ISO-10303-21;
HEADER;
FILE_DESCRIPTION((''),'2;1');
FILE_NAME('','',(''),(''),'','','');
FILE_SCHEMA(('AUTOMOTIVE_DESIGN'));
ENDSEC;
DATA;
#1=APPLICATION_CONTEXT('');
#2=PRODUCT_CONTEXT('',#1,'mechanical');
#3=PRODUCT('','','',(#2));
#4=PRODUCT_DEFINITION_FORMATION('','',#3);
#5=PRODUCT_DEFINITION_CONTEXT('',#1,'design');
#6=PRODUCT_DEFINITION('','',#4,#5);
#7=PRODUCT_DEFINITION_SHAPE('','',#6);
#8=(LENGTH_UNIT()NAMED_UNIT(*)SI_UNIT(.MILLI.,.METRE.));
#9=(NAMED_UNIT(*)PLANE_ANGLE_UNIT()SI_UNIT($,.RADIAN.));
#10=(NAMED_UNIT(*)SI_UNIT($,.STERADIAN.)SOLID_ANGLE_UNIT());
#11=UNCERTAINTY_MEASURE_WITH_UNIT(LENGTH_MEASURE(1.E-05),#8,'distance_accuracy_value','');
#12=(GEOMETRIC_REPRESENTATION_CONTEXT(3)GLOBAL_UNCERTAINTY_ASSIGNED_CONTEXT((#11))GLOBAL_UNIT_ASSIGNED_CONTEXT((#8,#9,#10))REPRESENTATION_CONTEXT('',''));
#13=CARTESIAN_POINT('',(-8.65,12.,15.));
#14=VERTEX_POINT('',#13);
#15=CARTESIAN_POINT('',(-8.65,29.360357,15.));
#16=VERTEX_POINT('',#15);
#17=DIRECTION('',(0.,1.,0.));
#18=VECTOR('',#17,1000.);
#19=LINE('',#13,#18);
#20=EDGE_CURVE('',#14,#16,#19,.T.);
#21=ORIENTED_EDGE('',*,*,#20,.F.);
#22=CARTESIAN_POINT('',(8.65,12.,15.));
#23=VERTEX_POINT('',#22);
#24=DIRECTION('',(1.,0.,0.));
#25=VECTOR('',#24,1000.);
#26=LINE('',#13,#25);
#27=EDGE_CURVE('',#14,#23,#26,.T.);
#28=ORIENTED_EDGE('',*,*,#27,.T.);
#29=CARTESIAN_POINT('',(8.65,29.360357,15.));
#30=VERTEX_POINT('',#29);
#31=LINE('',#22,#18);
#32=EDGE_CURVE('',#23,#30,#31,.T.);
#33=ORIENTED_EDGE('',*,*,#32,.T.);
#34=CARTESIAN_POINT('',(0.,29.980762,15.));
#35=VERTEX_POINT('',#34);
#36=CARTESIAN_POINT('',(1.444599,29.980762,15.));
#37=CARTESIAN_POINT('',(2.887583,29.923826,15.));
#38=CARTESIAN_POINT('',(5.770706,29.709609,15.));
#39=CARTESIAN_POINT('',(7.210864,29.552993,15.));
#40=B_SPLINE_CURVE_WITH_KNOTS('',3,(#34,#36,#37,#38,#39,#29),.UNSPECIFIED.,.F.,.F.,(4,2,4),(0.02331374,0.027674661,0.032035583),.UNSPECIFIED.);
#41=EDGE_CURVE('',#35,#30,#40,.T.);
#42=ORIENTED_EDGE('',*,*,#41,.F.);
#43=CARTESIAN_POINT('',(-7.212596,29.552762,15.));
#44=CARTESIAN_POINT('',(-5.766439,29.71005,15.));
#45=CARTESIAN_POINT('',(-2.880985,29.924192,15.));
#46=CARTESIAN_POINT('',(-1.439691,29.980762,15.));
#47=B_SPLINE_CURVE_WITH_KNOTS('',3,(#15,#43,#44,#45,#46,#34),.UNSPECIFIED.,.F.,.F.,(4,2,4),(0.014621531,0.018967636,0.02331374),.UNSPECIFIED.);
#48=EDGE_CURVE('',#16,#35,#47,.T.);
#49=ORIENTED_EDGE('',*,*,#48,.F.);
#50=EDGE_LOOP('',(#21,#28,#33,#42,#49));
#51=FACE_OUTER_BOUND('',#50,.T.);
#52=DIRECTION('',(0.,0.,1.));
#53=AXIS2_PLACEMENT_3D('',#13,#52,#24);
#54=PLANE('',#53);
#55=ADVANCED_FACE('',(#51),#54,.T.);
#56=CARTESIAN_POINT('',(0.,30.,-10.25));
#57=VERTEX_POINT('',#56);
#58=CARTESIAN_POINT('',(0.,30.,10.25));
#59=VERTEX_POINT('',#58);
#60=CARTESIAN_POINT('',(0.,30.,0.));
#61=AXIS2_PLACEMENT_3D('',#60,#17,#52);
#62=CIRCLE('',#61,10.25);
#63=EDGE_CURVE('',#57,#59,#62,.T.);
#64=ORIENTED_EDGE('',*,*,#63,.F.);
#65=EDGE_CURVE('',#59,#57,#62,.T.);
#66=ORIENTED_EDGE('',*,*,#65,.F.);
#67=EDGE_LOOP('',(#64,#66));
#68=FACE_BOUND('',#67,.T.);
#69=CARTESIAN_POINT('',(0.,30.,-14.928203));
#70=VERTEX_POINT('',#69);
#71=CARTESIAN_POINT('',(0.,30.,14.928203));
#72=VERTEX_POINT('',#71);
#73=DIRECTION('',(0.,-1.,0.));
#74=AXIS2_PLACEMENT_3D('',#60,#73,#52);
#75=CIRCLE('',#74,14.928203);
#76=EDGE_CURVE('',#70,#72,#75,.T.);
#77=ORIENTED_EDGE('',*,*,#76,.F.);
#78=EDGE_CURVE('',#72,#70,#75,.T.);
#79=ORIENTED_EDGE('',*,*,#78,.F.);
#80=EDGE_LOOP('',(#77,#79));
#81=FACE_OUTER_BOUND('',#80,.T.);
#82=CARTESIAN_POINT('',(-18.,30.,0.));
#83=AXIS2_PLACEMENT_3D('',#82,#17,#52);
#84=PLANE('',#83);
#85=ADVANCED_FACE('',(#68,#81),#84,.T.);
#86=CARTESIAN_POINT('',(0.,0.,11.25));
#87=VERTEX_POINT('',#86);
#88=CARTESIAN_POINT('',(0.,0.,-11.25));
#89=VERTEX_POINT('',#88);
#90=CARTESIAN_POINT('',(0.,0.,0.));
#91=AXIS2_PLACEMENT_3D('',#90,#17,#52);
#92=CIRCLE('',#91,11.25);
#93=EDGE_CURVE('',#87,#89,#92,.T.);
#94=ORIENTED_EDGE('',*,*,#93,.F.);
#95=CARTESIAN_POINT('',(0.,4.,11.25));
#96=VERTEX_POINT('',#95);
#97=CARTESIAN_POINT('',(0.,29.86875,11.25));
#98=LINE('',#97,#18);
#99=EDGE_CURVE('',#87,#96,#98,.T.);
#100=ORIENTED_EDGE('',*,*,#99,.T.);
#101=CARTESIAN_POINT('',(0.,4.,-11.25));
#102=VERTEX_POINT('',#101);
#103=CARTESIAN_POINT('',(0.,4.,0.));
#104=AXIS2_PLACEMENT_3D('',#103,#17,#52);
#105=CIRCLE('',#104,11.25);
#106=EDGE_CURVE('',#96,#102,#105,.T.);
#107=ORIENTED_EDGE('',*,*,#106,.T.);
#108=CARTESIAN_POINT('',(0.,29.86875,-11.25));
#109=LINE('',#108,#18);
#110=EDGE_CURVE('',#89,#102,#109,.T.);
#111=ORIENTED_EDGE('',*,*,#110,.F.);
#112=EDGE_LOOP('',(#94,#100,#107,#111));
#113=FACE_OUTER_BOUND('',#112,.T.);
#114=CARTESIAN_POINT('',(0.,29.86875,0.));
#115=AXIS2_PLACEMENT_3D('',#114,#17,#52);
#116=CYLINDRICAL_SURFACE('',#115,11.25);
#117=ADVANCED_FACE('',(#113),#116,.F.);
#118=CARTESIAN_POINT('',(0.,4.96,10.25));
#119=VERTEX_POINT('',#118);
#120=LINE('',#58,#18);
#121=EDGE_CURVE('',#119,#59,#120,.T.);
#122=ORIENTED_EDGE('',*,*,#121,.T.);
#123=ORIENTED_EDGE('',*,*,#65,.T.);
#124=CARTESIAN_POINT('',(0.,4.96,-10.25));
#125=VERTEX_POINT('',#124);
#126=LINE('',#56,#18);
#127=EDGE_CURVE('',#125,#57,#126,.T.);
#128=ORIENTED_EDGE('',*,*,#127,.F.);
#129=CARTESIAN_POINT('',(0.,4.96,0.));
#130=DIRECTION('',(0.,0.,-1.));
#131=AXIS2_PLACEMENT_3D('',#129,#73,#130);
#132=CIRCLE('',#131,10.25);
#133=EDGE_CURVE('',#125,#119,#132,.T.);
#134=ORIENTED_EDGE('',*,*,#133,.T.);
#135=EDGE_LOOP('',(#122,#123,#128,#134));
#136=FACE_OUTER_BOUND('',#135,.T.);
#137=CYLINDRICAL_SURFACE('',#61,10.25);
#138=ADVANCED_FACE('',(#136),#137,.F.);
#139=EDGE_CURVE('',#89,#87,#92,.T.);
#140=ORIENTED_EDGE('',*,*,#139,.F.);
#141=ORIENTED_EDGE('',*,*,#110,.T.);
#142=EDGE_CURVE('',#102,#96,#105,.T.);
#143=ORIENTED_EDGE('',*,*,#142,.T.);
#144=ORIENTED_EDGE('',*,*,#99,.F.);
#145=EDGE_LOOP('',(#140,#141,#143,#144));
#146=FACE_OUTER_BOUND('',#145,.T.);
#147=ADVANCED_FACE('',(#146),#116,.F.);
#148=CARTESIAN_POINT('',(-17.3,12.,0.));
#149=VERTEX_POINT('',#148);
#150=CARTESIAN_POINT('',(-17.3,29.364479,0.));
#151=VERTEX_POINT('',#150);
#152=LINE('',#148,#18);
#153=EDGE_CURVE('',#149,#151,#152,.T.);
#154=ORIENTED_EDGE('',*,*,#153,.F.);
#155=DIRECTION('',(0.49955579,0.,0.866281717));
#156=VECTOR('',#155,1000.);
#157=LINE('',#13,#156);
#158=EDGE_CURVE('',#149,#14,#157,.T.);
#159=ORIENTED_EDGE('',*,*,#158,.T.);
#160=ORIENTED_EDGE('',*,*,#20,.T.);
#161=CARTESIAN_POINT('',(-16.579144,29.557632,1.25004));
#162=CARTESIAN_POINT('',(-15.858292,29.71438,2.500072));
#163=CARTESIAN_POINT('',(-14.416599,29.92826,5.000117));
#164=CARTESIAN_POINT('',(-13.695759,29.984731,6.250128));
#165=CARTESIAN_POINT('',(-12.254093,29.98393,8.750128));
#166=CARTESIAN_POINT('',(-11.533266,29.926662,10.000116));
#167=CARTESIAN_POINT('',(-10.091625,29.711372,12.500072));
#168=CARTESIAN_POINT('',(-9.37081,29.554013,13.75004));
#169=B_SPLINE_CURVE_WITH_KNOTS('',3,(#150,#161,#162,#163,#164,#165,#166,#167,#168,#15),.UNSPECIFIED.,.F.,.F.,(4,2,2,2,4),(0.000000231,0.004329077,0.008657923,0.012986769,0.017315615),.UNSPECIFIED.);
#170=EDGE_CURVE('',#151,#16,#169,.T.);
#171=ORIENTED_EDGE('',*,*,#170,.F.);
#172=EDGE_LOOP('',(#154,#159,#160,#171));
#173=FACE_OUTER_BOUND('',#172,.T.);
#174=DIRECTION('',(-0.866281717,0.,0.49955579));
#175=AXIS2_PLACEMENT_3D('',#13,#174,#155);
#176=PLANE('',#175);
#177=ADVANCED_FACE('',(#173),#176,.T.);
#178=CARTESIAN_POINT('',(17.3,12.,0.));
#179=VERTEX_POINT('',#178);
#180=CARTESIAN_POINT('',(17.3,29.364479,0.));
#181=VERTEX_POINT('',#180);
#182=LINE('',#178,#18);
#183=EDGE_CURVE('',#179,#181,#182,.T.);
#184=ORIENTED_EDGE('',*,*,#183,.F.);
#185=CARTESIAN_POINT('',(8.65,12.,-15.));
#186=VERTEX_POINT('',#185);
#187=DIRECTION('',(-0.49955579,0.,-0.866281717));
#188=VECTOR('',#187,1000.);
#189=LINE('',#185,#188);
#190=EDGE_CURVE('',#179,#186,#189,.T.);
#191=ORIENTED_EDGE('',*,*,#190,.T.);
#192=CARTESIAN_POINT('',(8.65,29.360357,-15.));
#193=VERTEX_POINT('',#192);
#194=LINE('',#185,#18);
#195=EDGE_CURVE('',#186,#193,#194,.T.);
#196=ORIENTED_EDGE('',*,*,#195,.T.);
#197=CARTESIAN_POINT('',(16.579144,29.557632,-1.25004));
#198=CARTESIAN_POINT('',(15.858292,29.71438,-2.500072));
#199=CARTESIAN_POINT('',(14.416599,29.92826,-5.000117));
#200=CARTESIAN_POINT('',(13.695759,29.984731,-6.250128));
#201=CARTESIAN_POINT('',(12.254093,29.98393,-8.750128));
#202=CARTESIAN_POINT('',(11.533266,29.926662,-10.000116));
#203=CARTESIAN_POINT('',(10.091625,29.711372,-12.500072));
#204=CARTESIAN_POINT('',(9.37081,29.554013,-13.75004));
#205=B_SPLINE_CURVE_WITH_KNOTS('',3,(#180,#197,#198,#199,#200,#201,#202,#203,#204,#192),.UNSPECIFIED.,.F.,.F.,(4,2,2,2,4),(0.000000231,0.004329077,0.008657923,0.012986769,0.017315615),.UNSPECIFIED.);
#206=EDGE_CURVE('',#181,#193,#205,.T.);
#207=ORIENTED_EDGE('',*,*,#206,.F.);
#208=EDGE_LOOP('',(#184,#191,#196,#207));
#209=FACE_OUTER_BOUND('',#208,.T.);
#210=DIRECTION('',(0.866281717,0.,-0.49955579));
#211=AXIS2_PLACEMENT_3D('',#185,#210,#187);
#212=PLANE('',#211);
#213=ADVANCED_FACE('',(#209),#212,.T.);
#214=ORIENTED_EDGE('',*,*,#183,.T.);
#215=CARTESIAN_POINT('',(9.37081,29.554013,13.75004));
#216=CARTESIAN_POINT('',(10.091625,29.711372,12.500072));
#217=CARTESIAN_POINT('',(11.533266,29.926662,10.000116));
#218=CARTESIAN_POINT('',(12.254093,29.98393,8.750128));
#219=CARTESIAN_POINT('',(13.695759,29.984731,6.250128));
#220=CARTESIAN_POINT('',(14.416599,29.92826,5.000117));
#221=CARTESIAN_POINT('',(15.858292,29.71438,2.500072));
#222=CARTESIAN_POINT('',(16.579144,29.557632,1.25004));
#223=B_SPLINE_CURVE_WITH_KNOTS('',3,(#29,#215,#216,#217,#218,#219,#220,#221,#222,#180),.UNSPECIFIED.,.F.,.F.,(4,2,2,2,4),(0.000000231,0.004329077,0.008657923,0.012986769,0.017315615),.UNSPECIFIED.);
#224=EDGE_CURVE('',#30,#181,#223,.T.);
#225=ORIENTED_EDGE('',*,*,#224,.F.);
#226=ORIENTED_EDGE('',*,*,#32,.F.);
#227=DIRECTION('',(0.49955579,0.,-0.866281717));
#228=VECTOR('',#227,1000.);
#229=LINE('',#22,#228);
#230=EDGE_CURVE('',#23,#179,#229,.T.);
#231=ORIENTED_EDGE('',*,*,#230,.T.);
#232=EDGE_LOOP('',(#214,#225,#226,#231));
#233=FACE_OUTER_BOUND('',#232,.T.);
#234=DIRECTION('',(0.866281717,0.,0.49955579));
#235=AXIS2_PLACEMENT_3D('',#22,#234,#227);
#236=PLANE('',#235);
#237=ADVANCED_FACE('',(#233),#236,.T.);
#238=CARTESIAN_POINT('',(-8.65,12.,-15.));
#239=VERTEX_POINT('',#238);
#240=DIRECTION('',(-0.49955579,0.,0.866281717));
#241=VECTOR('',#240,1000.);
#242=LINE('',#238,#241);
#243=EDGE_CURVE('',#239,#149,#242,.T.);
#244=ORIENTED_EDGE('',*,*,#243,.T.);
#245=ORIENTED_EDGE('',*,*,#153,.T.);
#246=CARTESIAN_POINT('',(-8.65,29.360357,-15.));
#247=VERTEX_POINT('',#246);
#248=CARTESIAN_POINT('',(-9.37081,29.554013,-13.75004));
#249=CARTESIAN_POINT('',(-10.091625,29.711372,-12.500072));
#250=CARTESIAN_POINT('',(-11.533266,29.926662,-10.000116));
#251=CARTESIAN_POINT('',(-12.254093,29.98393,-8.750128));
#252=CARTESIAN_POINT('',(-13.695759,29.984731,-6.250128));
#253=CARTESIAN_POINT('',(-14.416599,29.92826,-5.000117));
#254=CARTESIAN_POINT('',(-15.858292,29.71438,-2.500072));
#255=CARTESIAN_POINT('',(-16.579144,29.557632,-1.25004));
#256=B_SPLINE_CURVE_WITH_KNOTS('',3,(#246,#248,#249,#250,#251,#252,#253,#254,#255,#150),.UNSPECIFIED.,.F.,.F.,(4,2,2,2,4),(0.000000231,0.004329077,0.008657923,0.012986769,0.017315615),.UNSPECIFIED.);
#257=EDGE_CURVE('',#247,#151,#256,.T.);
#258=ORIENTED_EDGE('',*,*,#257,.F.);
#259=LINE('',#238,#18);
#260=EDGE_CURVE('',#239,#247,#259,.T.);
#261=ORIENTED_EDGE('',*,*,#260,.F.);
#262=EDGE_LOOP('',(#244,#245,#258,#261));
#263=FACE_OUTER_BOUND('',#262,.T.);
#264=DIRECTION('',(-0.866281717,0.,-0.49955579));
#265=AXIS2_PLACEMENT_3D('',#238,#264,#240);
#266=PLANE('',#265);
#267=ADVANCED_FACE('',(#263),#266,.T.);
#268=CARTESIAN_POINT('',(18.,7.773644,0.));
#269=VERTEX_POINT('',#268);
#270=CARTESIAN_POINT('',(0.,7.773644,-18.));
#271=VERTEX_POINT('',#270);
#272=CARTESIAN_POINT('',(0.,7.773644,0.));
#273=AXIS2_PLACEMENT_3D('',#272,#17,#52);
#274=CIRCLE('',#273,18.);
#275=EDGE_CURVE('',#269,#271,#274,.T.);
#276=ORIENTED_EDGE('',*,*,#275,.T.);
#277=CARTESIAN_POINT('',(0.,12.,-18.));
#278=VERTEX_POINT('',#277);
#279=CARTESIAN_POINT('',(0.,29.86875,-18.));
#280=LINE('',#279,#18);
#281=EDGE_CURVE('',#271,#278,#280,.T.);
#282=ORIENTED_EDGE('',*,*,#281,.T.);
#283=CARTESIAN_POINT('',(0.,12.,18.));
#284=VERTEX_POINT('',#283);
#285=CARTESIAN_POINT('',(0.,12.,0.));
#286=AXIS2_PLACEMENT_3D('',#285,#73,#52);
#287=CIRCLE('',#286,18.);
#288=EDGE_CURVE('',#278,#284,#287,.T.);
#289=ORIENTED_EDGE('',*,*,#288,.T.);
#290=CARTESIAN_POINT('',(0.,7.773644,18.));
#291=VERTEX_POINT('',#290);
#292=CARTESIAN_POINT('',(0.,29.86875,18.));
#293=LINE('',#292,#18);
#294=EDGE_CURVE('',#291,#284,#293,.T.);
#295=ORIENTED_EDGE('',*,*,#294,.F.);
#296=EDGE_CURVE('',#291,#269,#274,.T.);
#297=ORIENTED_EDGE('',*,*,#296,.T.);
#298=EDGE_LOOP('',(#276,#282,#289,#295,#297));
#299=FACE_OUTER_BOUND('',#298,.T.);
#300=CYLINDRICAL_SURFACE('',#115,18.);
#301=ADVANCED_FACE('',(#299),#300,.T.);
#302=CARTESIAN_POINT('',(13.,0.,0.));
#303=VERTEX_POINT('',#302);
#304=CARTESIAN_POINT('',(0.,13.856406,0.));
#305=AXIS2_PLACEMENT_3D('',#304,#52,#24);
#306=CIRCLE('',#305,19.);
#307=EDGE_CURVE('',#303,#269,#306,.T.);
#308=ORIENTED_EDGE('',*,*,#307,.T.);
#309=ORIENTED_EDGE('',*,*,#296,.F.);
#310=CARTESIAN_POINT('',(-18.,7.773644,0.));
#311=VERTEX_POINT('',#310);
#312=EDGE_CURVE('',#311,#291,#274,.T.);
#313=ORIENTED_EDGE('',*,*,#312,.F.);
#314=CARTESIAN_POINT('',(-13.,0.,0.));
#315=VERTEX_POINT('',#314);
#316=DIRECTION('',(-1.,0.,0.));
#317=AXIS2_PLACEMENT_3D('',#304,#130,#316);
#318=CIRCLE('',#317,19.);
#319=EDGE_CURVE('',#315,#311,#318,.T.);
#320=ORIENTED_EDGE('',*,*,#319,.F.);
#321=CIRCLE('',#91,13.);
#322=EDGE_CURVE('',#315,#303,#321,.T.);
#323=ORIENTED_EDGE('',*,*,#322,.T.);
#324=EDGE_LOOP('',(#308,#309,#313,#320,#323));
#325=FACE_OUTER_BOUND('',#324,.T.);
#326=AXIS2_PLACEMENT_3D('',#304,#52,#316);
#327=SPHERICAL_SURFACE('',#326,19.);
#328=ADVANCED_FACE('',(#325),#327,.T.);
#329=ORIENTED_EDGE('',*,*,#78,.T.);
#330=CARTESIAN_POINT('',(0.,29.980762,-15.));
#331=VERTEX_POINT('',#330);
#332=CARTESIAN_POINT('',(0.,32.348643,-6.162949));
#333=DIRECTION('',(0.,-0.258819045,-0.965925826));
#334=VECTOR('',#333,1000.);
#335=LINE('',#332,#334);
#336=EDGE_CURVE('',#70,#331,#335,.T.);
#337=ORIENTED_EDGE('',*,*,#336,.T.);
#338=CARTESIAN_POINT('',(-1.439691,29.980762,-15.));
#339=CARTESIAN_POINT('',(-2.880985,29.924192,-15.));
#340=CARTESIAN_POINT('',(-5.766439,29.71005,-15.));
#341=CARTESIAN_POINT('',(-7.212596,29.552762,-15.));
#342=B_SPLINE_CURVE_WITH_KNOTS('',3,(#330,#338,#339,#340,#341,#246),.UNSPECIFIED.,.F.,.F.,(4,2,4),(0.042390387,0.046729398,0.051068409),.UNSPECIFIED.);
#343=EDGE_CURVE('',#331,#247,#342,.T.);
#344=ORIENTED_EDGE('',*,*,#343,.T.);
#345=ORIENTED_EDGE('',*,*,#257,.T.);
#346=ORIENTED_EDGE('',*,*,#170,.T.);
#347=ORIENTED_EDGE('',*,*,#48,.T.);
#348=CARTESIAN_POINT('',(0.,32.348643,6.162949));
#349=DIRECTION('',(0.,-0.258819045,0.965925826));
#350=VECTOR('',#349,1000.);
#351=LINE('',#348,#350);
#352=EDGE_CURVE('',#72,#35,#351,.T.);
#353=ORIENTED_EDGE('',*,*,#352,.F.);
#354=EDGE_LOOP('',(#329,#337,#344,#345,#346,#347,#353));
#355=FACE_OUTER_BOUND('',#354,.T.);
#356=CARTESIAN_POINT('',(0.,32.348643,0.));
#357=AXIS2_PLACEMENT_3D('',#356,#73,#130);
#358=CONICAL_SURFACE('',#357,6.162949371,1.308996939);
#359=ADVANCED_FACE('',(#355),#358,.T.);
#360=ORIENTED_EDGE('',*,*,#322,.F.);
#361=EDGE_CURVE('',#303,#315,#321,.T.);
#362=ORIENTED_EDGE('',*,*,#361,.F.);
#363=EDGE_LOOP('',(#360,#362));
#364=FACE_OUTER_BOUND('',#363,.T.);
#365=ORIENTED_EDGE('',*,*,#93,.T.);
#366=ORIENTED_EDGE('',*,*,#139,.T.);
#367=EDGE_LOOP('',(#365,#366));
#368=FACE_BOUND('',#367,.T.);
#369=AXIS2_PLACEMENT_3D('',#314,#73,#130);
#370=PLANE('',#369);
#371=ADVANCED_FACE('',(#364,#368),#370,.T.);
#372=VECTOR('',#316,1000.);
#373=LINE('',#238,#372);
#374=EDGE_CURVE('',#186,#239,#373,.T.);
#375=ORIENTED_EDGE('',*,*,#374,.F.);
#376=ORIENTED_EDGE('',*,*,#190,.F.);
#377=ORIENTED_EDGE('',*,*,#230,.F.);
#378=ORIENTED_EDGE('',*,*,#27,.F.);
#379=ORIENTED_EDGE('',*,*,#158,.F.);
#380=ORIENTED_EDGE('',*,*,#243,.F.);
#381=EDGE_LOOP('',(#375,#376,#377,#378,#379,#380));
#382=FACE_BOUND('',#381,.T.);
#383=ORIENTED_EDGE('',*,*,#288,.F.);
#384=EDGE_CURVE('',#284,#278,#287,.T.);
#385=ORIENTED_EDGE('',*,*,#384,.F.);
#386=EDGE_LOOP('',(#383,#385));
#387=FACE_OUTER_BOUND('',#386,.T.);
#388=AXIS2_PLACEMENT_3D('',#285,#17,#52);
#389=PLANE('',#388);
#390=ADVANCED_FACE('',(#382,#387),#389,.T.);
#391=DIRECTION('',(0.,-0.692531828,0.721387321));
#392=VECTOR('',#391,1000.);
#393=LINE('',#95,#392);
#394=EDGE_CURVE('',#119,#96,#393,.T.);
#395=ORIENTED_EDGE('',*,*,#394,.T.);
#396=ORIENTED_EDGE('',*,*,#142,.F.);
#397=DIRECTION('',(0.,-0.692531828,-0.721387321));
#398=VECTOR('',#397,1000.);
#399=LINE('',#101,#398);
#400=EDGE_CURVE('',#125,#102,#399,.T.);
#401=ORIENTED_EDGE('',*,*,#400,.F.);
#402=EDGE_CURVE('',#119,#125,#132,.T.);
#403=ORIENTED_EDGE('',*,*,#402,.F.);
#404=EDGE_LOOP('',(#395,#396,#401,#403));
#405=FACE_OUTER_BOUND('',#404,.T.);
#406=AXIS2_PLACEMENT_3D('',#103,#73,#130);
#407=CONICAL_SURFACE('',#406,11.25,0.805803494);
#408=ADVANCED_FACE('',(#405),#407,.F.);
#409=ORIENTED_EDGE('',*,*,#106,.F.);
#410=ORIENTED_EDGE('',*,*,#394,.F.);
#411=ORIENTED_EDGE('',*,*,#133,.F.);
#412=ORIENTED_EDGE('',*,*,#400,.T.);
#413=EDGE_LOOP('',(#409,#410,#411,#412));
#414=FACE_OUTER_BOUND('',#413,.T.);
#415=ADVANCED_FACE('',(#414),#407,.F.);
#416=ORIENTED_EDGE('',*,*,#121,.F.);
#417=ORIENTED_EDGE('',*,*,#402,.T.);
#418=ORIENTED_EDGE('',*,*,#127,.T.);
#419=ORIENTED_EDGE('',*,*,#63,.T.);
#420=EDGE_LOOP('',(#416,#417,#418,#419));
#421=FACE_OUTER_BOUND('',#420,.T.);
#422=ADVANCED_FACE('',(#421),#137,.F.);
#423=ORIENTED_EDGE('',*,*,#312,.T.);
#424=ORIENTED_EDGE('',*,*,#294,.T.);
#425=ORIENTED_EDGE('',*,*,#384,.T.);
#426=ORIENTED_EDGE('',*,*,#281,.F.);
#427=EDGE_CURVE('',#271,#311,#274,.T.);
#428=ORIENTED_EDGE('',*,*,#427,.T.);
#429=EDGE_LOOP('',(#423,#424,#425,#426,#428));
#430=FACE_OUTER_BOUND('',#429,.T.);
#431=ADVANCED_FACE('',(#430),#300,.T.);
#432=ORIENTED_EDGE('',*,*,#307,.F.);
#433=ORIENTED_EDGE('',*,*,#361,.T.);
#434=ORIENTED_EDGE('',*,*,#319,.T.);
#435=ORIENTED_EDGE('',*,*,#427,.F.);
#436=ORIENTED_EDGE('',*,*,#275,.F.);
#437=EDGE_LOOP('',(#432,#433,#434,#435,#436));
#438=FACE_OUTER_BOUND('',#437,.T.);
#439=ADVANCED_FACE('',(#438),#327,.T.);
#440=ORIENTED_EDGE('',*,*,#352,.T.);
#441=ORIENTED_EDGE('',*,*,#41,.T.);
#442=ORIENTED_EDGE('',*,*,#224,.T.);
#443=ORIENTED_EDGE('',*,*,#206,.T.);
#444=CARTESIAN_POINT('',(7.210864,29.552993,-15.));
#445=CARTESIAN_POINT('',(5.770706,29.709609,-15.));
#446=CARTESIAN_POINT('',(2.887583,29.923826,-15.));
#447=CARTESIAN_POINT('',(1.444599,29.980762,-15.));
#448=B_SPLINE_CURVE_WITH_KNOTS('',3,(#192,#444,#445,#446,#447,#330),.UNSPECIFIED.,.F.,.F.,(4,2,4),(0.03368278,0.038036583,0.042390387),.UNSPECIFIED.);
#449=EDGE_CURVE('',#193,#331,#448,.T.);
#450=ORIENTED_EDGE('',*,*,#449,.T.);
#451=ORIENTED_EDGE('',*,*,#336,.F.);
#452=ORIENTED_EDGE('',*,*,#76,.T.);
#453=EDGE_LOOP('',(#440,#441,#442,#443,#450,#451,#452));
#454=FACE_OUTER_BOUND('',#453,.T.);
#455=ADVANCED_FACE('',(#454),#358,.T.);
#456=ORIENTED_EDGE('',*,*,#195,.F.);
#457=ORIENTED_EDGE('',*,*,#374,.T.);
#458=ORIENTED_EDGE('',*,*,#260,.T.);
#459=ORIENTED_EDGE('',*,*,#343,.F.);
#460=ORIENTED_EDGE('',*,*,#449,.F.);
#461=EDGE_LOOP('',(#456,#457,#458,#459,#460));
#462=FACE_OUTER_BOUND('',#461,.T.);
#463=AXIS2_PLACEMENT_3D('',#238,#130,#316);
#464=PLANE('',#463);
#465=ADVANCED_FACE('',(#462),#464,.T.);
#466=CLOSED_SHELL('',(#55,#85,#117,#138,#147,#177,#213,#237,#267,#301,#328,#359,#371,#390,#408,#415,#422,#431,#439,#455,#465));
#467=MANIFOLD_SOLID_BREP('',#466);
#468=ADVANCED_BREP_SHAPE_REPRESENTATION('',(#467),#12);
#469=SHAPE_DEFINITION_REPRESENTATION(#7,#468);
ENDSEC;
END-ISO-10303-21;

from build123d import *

# Parameters (mm, degrees)
M22X1_5_1_D         = 20.5
SKETCH_4_OUTSIDE_W  = 49.818
SKETCH_4_OUTSIDE_H  = 49.818
CUT_EXTRUDE_1_DEPTH = 18


with BuildPart() as part:
    # 草图1 → 旋转1 (revolve)
    with BuildSketch(Plane.XY, mode=Mode.PRIVATE) as revolve_1_sk:
        with BuildLine():
            Line((-18, 7.77364393), (-18, 30))
            Line((-18, 30), (-10, 30))
            Line((-10, 30), (-10, 5.2))
            Line((-10, 5.2), (-11.25, 4))
            Line((-11.25, 4), (-11.25, 0))
            Line((-11.25, 0), (-13, 0))
            ThreePointArc((-13, 0), (-15.979905663, 3.578147123), (-18, 7.77364393))
        make_face()
    revolve(revolve_1_sk.sketch.rotate(Axis((0, 29.86875, 0), (0, -1, 0)), 270), axis=Axis((0, 29.86875, 0), (0, -1, 0)))

    # M22x1.5 螺纹孔1 (through all)
    with Locations(Plane(origin=(0, 30, 0), x_dir=(1, 0, 0), z_dir=(0, 1, 0))):
        with Locations((0, 0)):
            Hole(M22X1_5_1_D / 2)

    # 草图4 outside → 切除-拉伸1 (cut)
    with BuildSketch(Plane(origin=(0, 30, 0), x_dir=(1, 0, 0), z_dir=(0, 1, 0))):
        Rectangle(SKETCH_4_OUTSIDE_W, SKETCH_4_OUTSIDE_H)
        Polygon((-8.65, 15), (8.65, 15), (17.3, 0), (8.65, -15), (-8.65, -15), (-17.3, 0), align=None, mode=Mode.SUBTRACT)
    extrude(amount=-CUT_EXTRUDE_1_DEPTH, mode=Mode.SUBTRACT)

    # 草图6 → 切除-旋转8 (revolve, cut)
    with BuildSketch(Plane(origin=(0, 0, 0), x_dir=(0, 0, -1), z_dir=(1, 0, 0)), mode=Mode.PRIVATE) as cut_revolve_8_sk:
        Polygon((6.162949371, 32.348642693), (24.147556169, 27.529681825), (24.147556169, 34), (6.162949371, 34), align=None)
    revolve(cut_revolve_8_sk.sketch.rotate(Axis((0, 32.348642693, 0), (0, 1, 0)), 90), axis=Axis((0, 32.348642693, 0), (0, 1, 0)), mode=Mode.SUBTRACT)


solid = part.part
